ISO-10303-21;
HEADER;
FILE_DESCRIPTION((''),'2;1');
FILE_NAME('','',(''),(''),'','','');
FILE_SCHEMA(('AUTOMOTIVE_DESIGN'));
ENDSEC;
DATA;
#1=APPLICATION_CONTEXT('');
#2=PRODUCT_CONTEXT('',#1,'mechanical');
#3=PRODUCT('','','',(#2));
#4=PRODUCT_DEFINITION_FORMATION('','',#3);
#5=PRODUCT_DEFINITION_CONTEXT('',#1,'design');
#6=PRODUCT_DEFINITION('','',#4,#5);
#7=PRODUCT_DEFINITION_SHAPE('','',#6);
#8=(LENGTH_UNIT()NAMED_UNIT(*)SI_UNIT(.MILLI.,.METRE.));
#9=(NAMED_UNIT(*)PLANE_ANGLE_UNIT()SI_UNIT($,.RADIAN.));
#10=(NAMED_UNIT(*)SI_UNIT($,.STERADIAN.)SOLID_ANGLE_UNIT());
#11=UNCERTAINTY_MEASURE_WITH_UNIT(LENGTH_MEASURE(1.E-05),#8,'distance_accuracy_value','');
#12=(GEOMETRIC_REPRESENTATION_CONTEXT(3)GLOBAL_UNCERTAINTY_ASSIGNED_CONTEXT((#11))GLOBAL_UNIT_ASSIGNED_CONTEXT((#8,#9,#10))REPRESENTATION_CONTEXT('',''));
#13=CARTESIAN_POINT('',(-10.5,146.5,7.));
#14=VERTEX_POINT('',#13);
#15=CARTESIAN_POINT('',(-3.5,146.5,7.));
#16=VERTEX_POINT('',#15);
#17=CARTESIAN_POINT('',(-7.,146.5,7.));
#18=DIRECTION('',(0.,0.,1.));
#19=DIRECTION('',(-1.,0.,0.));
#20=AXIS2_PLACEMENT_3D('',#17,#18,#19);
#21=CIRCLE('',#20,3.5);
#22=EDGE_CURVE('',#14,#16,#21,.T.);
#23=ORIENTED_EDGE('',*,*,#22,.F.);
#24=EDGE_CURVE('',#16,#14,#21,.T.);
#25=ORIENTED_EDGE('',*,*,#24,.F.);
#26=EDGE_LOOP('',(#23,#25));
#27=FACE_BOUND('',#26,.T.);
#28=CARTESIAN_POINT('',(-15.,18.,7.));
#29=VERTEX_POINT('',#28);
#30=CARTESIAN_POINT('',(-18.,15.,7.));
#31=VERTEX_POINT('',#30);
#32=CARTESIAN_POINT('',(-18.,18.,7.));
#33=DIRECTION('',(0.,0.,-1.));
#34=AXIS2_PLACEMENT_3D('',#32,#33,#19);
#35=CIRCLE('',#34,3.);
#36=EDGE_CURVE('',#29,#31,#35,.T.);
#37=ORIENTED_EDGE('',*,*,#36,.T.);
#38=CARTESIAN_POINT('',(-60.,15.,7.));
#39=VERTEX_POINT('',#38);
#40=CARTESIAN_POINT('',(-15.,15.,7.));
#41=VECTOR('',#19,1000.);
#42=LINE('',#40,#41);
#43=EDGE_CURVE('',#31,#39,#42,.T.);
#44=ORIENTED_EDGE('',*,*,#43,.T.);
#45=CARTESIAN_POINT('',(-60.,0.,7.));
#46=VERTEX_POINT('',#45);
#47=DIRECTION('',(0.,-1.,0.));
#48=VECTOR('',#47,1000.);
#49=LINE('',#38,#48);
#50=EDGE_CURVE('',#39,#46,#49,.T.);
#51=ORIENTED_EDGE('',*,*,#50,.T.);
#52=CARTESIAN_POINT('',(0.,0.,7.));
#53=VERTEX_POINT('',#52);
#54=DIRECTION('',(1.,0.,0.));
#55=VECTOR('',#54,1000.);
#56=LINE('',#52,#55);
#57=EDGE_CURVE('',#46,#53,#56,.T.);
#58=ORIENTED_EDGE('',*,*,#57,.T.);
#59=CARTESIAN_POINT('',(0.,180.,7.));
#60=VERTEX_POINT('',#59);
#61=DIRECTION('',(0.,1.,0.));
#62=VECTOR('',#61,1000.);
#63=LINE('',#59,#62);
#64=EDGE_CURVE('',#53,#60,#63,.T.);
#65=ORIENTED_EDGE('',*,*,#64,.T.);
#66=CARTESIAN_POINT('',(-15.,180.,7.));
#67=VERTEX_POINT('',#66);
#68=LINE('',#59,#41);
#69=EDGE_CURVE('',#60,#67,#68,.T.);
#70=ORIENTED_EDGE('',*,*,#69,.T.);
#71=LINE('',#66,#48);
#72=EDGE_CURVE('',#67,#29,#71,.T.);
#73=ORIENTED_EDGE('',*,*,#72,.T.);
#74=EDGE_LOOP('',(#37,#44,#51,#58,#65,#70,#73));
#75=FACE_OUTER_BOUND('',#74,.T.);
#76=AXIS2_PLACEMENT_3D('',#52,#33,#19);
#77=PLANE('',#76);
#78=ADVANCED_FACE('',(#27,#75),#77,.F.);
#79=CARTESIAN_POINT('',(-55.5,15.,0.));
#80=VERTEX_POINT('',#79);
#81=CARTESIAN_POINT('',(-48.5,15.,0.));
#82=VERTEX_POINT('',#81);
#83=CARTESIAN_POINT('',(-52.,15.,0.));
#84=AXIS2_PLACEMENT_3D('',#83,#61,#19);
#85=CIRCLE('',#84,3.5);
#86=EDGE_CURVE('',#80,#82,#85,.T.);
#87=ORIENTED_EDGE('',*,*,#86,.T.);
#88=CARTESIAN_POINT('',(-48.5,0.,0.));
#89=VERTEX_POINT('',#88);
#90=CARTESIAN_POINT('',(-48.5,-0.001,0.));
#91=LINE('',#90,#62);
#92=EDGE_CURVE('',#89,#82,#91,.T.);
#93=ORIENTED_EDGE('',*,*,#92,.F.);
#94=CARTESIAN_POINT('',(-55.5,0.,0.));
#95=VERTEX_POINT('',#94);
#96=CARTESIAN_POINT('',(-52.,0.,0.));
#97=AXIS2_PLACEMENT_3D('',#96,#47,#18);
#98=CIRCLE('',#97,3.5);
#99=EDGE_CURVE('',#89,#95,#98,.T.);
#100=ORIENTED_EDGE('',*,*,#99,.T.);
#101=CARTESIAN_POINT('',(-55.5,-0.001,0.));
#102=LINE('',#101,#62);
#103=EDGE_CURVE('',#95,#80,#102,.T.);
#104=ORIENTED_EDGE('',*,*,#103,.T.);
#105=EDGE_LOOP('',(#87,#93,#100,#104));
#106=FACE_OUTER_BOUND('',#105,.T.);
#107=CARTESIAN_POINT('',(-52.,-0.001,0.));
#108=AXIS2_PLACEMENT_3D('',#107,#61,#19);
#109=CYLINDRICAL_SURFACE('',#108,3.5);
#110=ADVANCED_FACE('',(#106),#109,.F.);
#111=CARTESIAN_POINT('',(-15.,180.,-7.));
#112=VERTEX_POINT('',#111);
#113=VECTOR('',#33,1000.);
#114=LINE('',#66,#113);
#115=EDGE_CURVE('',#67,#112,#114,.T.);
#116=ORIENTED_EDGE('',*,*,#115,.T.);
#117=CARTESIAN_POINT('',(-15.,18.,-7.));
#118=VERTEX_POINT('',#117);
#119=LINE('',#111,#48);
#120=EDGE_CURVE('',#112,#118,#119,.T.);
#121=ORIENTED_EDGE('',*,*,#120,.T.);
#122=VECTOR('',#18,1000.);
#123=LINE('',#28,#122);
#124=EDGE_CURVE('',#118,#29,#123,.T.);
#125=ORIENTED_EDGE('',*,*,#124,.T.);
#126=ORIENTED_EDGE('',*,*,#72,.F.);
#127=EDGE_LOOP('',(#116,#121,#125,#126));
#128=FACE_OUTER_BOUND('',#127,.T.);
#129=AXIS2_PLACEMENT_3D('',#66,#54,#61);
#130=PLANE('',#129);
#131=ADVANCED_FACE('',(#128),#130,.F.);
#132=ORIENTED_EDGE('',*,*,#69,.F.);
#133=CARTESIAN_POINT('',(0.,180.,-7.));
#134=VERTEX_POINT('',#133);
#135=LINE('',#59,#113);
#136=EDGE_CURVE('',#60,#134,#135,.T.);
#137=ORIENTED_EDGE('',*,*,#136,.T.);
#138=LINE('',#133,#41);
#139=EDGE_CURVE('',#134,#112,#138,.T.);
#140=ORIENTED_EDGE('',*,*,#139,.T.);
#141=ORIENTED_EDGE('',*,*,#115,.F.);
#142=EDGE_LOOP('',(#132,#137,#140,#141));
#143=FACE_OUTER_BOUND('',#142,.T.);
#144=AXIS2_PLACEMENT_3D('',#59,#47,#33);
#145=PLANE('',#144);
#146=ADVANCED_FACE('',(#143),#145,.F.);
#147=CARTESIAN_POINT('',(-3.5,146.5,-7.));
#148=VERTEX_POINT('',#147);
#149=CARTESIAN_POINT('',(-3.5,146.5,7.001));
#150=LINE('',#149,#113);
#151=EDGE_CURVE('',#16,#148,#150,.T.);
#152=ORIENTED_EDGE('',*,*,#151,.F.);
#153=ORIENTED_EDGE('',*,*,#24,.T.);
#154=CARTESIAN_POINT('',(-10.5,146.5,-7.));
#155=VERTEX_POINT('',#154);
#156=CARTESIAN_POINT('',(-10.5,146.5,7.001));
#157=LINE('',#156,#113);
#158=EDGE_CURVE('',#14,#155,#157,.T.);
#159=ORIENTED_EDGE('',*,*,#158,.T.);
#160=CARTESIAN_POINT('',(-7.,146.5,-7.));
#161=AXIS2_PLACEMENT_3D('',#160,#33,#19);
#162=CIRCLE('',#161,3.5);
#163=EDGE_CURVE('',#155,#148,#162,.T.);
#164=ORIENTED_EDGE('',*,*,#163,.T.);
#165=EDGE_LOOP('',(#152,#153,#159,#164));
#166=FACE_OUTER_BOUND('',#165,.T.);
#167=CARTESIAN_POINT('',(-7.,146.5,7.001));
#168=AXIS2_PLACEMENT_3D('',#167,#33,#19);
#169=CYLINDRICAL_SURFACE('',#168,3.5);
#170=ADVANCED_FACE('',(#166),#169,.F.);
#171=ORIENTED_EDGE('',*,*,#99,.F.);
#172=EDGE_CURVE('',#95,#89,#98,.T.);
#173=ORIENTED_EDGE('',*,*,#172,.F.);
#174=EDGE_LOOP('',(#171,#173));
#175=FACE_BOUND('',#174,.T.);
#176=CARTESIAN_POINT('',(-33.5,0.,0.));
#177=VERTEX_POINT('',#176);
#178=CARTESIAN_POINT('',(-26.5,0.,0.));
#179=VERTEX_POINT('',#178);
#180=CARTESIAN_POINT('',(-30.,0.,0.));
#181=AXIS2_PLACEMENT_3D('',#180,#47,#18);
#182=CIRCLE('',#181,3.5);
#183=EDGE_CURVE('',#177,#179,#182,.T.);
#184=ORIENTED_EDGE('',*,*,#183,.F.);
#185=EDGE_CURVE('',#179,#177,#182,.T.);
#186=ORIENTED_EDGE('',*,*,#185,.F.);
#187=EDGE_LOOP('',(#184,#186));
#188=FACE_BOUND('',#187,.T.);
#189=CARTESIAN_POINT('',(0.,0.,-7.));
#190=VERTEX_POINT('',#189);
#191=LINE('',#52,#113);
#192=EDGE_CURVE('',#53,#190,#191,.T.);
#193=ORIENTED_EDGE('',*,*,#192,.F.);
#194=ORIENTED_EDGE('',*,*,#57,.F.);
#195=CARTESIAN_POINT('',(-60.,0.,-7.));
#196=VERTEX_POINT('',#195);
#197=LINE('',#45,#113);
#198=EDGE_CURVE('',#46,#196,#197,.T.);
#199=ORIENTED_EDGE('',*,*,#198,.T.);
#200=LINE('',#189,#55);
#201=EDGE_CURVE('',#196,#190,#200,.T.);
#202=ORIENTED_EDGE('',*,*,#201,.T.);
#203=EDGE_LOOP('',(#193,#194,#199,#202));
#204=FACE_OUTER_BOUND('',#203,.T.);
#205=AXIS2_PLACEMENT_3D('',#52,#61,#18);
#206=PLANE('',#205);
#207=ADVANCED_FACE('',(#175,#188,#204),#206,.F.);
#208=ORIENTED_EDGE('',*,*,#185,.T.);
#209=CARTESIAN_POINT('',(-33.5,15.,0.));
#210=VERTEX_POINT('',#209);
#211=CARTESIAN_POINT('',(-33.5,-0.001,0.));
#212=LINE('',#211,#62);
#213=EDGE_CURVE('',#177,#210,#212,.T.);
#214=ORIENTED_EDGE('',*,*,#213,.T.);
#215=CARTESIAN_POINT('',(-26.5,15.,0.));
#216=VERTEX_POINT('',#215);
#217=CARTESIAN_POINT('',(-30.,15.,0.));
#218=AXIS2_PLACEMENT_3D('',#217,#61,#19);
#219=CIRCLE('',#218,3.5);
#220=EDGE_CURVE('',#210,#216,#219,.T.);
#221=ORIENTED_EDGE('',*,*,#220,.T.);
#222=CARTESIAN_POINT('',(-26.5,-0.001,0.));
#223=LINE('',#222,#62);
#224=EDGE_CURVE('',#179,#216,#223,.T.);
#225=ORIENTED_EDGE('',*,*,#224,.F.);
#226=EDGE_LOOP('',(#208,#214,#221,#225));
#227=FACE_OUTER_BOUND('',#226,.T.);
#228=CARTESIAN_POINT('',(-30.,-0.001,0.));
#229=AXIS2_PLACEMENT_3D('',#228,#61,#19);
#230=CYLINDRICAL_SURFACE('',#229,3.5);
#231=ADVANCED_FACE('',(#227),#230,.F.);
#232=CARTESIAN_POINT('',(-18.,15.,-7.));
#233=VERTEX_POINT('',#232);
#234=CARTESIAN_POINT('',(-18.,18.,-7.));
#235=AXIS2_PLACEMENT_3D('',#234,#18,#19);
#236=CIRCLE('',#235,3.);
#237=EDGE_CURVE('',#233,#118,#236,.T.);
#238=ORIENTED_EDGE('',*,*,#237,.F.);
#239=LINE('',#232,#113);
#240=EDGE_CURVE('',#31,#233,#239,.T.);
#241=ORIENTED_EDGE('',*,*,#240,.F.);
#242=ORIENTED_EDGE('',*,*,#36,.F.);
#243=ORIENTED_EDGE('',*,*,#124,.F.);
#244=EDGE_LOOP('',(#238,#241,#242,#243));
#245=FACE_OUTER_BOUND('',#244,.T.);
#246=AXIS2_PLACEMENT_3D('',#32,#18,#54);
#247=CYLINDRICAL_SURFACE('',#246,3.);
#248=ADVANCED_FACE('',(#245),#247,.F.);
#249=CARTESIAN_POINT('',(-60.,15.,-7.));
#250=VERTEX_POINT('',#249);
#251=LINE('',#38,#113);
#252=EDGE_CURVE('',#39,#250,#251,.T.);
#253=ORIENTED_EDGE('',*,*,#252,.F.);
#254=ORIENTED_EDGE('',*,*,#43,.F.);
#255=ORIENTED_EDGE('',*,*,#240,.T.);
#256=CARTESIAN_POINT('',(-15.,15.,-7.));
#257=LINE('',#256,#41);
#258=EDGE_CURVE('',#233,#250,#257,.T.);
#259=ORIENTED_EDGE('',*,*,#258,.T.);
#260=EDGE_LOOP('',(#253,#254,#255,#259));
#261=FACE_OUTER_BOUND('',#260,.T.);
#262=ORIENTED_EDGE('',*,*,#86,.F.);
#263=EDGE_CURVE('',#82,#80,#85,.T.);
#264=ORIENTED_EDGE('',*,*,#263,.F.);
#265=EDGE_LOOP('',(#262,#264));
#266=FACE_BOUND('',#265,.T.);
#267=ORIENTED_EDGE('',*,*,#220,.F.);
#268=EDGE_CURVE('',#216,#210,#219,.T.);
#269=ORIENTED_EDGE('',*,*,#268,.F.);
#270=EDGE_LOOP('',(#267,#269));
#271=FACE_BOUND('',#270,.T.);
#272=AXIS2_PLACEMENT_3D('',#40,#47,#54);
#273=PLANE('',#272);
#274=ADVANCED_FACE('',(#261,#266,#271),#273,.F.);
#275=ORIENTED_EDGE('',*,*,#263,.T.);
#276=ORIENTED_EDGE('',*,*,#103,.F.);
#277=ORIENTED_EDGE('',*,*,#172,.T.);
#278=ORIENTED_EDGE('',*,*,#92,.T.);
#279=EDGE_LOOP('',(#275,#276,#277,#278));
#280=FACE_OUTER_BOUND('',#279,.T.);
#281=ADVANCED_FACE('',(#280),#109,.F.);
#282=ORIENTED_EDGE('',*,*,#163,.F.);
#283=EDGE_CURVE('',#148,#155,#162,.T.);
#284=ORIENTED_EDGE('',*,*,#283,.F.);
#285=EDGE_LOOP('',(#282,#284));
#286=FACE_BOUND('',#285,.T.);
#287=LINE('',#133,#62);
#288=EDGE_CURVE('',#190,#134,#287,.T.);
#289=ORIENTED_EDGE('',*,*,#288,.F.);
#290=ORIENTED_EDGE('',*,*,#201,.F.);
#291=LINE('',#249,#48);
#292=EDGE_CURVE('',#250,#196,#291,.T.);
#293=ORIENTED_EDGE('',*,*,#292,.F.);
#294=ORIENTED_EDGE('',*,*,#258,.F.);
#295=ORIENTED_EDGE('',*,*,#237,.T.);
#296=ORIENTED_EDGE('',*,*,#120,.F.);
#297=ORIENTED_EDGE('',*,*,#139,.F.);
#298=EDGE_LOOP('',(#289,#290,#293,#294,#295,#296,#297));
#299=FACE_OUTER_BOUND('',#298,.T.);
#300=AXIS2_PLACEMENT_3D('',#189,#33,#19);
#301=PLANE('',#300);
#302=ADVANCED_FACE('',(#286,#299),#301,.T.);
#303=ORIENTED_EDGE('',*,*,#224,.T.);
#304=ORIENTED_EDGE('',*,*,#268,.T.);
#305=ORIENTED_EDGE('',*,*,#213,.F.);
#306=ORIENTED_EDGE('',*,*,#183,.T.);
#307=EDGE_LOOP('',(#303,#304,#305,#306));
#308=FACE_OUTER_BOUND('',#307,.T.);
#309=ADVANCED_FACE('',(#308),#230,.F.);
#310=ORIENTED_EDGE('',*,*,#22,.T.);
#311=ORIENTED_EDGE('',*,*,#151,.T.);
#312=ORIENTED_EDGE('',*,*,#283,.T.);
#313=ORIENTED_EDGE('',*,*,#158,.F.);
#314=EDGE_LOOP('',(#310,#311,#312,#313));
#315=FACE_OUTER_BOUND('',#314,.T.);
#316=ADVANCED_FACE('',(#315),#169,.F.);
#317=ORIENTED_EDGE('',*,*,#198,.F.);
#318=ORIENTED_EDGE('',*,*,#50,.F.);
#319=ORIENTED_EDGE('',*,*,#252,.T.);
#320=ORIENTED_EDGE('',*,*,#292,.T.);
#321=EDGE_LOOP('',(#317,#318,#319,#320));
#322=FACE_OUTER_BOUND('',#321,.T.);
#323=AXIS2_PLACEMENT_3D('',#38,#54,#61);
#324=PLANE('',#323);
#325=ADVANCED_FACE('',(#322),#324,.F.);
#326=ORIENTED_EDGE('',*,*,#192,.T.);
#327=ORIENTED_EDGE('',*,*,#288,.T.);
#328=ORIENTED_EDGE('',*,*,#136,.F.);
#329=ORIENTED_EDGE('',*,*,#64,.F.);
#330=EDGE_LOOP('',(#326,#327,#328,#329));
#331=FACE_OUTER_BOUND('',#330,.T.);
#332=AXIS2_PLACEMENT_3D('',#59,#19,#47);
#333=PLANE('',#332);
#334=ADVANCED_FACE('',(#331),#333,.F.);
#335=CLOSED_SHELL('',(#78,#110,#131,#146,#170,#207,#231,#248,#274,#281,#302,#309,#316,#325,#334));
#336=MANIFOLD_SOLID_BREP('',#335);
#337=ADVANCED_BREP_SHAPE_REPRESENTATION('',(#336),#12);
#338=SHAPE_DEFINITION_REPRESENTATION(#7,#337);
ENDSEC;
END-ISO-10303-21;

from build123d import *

# Parameters (mm, degrees)
EXTRUDE_1_DEPTH     = 7
FILLET_1_R          = 3
CUT_EXTRUDE_1_REACH = 177.71
SKETCH_3_R          = 3.5
CUT_EXTRUDE_2_REACH = 192.252
SKETCH_4_R          = 3.5


with BuildPart() as part:
    # 草图1 → 凸台-拉伸1 (new, symmetric)
    with BuildSketch(Plane.XY):
        Polygon((0, 180), (-15, 180), (-15, 15), (-60, 15), (-60, 0), (0, 0), align=None)
    extrude(amount=EXTRUDE_1_DEPTH, both=True)

    # 圆角1
    fillet_1_edges = [part.edges().sort_by_distance(p)[0] for p in [
        (-15, 15, 0),
    ]]
    fillet(fillet_1_edges, radius=FILLET_1_R)

    # 草图3 → 切除-拉伸1 (cut, up to next)
    with BuildSketch(Plane(origin=(0, 15, 0), x_dir=(1, 0, 0), z_dir=(0, 1, 0)), mode=Mode.PRIVATE) as cut_extrude_1_sk1:
        with Locations(Location((-52, 0, 0), (0, 0, 180))):
            Circle(SKETCH_3_R)
    cut_extrude_1_tool1 = extrude(cut_extrude_1_sk1.sketch, amount=-CUT_EXTRUDE_1_REACH, mode=Mode.PRIVATE) & part.part
    # 草图3 → 切除-拉伸1 (cut, up to next)
    with BuildSketch(Plane(origin=(0, 15, 0), x_dir=(1, 0, 0), z_dir=(0, 1, 0)), mode=Mode.PRIVATE) as cut_extrude_1_sk2:
        with Locations(Location((-30, 0, 0), (0, 0, 180))):
            Circle(SKETCH_3_R)
    cut_extrude_1_tool2 = extrude(cut_extrude_1_sk2.sketch, amount=-CUT_EXTRUDE_1_REACH, mode=Mode.PRIVATE) & part.part
    add(cut_extrude_1_tool1.solids().sort_by_distance((-52, 15, 0))[0], mode=Mode.SUBTRACT)
    add(cut_extrude_1_tool2.solids().sort_by_distance((-30, 15, 0))[0], mode=Mode.SUBTRACT)

    # 草图4 → 切除-拉伸2 (cut, up to next)
    with BuildSketch(Plane(origin=(0, 0, -7), x_dir=(-1, 0, 0), z_dir=(0, 0, -1)), mode=Mode.PRIVATE) as cut_extrude_2_sk1:
        with Locations((7, 146.5)):
            Circle(SKETCH_4_R)
    cut_extrude_2_tool1 = extrude(cut_extrude_2_sk1.sketch, amount=-CUT_EXTRUDE_2_REACH, mode=Mode.PRIVATE) & part.part
    add(cut_extrude_2_tool1.solids().sort_by_distance((-7, 146.5, -7))[0], mode=Mode.SUBTRACT)


solid = part.part
